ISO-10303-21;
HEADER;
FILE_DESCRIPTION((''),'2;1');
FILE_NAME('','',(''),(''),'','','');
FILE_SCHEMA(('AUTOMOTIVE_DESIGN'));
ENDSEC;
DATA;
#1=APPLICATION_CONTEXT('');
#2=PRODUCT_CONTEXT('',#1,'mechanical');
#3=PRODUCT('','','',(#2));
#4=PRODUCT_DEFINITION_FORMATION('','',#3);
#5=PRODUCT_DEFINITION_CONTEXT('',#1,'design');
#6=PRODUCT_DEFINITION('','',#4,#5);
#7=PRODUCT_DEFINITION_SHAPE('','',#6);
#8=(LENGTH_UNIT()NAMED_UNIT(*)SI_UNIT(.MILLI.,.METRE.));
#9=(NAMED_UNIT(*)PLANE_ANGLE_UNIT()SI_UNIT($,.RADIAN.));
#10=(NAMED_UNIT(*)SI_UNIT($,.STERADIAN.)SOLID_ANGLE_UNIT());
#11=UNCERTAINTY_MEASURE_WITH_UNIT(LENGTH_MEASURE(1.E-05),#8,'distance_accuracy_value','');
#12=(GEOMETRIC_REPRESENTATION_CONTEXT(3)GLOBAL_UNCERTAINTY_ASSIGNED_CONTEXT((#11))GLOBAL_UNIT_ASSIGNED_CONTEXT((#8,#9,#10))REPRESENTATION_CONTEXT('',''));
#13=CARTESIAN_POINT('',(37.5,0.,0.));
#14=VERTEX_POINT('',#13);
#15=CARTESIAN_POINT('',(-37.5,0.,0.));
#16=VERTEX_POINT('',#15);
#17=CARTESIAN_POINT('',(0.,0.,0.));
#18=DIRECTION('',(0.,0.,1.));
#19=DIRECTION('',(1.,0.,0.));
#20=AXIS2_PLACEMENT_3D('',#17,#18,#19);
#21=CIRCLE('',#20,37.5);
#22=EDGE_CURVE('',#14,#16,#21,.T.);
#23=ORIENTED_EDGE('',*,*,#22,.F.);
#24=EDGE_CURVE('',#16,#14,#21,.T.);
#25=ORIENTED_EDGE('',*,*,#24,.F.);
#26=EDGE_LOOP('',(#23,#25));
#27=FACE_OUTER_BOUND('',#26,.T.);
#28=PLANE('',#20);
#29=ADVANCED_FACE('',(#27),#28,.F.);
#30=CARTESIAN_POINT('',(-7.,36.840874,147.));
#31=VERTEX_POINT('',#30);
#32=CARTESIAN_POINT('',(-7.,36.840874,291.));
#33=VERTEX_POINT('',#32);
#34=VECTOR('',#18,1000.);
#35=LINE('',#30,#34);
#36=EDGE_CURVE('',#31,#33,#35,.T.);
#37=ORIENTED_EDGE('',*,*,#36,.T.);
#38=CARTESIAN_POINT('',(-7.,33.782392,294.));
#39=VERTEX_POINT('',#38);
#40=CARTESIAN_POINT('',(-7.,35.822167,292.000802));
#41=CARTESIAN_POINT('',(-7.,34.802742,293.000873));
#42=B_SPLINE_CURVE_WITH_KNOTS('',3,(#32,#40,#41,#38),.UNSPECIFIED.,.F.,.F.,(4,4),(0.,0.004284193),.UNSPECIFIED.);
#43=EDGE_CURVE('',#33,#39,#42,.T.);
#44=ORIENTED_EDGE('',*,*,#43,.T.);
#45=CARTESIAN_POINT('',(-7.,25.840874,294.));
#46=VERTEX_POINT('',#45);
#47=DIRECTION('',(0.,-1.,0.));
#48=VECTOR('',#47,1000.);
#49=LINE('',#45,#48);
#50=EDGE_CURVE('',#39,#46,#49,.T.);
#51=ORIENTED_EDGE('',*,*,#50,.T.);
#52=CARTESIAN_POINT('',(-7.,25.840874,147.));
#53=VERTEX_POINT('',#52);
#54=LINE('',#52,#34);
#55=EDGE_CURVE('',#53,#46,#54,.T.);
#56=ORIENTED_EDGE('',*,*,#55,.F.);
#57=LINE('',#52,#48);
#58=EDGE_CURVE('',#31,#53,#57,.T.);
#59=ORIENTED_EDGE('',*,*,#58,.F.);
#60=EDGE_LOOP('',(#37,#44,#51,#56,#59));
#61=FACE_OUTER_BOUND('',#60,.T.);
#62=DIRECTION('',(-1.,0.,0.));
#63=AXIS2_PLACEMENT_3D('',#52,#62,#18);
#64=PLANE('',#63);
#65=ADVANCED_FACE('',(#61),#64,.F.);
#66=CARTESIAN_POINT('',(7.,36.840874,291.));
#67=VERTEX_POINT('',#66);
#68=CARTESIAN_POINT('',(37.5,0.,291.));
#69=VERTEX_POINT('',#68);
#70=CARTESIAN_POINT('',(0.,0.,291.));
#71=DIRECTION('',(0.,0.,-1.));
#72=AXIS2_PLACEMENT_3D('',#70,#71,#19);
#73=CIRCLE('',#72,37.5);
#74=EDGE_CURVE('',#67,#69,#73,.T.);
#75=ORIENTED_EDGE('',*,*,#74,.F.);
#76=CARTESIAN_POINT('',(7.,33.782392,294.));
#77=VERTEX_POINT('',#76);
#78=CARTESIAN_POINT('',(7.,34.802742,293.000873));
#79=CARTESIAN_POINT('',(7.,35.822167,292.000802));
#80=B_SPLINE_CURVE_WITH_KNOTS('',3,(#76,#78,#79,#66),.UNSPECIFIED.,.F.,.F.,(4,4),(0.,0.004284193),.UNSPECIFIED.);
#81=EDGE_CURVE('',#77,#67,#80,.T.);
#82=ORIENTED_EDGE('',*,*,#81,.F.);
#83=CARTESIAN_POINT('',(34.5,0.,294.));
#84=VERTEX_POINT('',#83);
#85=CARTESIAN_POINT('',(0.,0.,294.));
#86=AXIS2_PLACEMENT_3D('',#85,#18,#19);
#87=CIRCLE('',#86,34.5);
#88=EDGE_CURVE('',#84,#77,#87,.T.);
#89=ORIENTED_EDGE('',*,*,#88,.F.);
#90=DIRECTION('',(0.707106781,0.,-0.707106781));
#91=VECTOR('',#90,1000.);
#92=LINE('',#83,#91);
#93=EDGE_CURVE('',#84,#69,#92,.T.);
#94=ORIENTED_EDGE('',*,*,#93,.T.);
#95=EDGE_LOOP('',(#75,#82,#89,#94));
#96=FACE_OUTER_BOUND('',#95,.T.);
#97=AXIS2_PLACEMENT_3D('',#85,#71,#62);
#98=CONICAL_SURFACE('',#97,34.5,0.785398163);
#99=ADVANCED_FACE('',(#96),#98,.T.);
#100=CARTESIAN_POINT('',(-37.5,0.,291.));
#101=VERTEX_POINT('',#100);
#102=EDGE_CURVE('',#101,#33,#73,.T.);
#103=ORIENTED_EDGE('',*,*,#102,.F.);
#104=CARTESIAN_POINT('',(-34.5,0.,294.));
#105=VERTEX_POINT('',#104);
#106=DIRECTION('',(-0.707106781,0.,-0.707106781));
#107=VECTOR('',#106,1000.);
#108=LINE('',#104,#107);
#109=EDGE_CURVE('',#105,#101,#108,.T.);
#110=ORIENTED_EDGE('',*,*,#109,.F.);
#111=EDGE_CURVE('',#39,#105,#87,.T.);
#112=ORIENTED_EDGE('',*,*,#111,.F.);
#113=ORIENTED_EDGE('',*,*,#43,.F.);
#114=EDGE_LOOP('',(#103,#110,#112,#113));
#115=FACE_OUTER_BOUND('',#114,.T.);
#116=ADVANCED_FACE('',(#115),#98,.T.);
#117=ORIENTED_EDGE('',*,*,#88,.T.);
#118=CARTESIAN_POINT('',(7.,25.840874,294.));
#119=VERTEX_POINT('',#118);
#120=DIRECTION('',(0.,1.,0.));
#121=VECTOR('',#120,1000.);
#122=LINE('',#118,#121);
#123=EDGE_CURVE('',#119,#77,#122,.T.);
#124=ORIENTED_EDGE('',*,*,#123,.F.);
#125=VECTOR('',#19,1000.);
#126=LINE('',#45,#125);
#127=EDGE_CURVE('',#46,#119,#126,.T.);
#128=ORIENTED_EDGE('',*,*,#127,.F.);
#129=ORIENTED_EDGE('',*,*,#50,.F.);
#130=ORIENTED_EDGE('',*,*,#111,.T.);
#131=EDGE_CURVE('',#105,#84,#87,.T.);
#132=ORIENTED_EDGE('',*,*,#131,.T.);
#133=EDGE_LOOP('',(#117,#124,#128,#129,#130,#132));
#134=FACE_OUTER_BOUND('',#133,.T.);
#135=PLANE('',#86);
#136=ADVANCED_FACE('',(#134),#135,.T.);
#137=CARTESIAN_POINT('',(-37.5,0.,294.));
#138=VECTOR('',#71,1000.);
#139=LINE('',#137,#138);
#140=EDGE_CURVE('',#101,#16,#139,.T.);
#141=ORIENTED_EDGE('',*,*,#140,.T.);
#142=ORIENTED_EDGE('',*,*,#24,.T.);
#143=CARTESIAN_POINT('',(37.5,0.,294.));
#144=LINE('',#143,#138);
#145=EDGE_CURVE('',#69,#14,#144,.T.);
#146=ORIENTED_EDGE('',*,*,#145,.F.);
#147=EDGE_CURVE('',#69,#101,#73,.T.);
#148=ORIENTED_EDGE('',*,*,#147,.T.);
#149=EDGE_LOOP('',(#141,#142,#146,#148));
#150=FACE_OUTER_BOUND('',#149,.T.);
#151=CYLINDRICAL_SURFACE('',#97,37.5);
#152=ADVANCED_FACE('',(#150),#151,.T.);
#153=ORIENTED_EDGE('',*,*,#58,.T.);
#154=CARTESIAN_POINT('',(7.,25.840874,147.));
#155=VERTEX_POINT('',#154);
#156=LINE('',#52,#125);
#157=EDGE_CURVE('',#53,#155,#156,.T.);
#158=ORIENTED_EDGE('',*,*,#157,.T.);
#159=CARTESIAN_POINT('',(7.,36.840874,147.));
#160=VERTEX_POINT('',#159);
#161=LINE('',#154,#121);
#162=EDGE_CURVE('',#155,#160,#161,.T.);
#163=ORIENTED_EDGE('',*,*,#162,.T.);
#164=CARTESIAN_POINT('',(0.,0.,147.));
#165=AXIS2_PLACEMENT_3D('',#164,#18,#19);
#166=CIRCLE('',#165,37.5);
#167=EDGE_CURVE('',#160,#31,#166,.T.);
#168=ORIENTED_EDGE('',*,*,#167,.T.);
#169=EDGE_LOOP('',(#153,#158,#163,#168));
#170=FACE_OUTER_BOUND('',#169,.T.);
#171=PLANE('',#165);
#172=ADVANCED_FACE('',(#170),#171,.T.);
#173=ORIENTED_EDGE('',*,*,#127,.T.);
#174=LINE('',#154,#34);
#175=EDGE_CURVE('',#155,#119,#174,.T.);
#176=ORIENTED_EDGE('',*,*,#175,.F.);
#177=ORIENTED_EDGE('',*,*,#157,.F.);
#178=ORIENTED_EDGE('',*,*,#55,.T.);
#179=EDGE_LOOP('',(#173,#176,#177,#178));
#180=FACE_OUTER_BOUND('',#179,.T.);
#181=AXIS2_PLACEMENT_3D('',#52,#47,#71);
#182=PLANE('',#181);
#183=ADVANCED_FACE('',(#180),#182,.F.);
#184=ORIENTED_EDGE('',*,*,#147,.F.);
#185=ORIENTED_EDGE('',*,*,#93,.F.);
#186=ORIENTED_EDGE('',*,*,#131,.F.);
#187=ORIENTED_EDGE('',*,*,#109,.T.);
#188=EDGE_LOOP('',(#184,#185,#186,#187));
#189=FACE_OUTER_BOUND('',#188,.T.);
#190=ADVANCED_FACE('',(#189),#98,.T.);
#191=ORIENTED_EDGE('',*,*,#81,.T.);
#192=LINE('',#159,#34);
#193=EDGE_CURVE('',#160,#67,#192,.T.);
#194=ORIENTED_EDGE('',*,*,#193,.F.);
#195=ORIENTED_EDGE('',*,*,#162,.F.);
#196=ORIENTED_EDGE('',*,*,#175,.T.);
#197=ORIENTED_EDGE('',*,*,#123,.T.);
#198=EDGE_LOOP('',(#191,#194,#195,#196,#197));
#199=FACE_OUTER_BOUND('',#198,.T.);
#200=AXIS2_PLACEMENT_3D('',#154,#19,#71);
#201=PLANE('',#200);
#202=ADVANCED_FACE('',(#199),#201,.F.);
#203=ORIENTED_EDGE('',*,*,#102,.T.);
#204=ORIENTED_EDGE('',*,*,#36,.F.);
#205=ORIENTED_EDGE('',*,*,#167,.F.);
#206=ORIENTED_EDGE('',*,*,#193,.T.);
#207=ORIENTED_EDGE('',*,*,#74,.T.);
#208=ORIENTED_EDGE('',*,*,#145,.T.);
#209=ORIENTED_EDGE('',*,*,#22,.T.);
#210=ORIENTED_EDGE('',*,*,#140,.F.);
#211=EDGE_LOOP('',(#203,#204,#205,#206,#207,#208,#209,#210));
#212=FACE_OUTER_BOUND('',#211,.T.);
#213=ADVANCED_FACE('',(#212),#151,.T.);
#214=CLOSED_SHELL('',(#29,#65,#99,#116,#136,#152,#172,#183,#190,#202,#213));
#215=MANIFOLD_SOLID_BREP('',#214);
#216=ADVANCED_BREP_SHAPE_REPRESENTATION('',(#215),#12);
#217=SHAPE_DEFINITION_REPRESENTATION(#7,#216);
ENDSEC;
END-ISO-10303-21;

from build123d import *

# Parameters (mm, degrees)
SHAFT_PROFILE_75_R      = 37.5
SHAFT_BODY_75X294_DEPTH = 294
KEYWAY_START            = -147
KEYWAY_CUT_14X147_DEPTH = 147
END_CHAMFER_3X45_SIZE   = 3


with BuildPart() as part:
    # Shaft Profile Ø75 → Shaft Body Ø75x294 (new body)
    with BuildSketch(Plane.XY):
        Circle(SHAFT_PROFILE_75_R)
    extrude(amount=SHAFT_BODY_75X294_DEPTH)

    # Keyway Profile 14 wide → Keyway Cut 14x147 (cut)
    with BuildSketch(Plane.XY.offset(294).offset(KEYWAY_START)):
        with BuildLine():
            Line((-7, 25.84087404), (7, 25.84087404))
            Line((7, 25.84087404), (7, 36.84087404))
            ThreePointArc((7, 36.84087404), (0, 37.5), (-7, 36.84087404))
            Line((-7, 36.84087404), (-7, 25.84087404))
        make_face()
    extrude(amount=KEYWAY_CUT_14X147_DEPTH, mode=Mode.SUBTRACT)

    # End Chamfer 3x45°
    end_chamfer_3x45_edges = [part.edges().sort_by_distance(p)[0] for p in [
        (-23.913908087, -28.885550021, 294),
    ]]
    chamfer(end_chamfer_3x45_edges, length=END_CHAMFER_3X45_SIZE)


solid = part.part
